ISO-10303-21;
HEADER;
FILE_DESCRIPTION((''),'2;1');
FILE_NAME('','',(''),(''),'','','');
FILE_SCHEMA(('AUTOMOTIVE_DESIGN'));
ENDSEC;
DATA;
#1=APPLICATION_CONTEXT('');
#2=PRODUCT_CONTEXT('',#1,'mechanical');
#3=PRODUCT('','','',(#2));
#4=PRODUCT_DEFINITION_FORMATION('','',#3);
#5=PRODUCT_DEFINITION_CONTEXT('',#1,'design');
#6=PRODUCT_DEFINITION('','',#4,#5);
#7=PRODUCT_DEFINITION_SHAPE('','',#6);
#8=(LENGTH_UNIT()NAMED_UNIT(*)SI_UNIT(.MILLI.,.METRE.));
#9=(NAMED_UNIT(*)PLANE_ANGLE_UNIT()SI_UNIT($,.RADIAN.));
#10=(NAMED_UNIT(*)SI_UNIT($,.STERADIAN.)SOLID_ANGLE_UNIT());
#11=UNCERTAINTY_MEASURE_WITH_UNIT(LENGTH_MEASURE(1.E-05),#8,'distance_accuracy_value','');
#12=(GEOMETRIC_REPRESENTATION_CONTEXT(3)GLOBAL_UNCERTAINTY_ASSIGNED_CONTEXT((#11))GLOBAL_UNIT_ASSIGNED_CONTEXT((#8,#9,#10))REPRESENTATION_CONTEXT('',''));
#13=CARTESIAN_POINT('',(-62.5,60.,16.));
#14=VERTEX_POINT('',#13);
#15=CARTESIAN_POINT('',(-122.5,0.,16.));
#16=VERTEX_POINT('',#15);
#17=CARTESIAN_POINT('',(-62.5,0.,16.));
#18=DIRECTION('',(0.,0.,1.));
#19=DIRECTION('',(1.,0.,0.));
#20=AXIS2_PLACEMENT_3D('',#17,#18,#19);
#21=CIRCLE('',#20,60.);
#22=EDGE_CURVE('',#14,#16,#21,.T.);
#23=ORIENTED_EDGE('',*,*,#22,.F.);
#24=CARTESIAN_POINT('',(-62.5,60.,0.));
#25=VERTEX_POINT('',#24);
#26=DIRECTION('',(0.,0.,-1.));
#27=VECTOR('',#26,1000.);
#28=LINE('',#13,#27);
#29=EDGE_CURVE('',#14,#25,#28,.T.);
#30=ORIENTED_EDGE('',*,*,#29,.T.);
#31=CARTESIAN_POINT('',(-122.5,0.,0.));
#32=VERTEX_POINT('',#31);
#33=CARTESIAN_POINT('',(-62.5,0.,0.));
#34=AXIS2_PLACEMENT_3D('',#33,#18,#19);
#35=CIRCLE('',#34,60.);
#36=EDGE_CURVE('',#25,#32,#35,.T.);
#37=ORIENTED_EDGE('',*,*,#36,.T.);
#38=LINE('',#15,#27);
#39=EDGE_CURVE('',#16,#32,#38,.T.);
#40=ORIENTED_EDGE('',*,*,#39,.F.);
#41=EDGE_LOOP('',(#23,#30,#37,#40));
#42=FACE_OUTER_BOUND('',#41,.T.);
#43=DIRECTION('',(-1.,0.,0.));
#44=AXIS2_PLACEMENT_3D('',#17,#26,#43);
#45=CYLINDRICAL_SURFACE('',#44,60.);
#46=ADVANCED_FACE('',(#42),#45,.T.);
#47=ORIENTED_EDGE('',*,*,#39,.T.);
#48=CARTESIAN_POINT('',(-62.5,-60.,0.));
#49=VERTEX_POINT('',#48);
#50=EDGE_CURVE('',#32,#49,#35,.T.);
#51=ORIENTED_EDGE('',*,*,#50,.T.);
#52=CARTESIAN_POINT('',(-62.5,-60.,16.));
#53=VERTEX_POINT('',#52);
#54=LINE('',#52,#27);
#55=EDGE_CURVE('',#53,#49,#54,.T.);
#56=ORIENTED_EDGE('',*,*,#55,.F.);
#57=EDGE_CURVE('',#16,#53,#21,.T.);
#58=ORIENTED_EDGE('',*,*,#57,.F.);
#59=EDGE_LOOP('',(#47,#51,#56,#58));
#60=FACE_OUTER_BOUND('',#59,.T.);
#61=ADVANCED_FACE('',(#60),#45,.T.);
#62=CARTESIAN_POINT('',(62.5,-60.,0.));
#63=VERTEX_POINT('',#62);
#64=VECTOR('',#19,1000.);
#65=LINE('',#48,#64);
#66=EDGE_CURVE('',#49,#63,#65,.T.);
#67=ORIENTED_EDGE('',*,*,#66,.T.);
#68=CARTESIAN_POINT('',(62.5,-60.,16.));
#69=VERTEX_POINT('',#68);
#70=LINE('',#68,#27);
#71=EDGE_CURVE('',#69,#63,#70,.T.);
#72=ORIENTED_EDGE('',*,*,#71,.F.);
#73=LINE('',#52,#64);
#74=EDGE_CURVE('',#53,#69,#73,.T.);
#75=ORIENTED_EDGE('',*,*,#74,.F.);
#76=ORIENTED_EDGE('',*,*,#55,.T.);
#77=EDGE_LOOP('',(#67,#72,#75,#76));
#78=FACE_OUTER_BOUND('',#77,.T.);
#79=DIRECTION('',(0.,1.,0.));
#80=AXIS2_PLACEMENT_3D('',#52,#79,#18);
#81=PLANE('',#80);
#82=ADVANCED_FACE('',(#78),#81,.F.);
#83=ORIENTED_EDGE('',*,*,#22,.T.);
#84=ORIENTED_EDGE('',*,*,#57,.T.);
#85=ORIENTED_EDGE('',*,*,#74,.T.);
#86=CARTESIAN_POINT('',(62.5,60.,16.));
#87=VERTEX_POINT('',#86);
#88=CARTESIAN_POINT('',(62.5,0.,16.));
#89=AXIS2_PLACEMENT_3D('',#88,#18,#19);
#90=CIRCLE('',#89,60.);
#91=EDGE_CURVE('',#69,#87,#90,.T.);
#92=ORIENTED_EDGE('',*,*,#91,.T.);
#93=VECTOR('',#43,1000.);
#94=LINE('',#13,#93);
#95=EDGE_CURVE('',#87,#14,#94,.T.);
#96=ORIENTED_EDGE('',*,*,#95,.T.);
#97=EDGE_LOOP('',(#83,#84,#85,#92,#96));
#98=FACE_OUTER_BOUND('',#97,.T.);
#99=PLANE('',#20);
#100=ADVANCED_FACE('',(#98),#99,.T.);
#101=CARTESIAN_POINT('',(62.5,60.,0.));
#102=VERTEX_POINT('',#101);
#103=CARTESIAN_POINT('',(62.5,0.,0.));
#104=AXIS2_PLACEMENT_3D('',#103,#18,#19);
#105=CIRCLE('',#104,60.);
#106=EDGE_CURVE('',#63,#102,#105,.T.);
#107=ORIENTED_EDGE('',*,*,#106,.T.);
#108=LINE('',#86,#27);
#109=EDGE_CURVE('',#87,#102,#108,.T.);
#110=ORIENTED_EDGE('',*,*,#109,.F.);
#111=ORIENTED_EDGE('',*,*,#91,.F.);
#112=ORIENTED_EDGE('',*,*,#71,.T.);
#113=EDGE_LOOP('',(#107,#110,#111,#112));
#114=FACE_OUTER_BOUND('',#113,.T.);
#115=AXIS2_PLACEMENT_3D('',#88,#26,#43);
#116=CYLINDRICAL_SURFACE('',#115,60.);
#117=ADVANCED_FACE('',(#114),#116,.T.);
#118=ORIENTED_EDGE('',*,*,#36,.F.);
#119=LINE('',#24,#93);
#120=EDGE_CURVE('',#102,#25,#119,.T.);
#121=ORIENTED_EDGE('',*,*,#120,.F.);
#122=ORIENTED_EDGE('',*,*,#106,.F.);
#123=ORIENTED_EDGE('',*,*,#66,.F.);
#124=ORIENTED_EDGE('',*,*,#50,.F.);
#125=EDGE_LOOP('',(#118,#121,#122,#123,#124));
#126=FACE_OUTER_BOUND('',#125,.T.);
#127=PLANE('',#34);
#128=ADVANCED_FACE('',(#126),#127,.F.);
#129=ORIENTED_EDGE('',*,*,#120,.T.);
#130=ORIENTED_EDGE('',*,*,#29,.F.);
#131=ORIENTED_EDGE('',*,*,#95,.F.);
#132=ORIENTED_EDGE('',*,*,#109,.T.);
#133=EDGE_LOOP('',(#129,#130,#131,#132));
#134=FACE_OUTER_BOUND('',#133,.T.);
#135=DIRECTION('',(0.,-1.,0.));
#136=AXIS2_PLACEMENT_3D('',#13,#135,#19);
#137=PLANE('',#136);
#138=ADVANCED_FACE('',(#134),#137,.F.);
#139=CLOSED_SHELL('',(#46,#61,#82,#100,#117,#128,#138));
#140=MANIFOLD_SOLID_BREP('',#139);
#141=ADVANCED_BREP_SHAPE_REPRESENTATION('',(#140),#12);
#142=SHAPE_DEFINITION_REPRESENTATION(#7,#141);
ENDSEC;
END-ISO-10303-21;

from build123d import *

# Parameters (mm, degrees)
EXTRUDE_1_DEPTH = 16


with BuildPart() as part:
    # 草图1 → 凸台-拉伸1 (new body)
    with BuildSketch(Plane.XY):
        with BuildLine():
            Line((-62.5, 60), (62.5, 60))
            ThreePointArc((62.5, 60), (122.5, 0), (62.5, -60))
            Line((62.5, -60), (-62.5, -60))
            ThreePointArc((-62.5, -60), (-122.5, 0), (-62.5, 60))
        make_face()
    extrude(amount=EXTRUDE_1_DEPTH)


solid = part.part
